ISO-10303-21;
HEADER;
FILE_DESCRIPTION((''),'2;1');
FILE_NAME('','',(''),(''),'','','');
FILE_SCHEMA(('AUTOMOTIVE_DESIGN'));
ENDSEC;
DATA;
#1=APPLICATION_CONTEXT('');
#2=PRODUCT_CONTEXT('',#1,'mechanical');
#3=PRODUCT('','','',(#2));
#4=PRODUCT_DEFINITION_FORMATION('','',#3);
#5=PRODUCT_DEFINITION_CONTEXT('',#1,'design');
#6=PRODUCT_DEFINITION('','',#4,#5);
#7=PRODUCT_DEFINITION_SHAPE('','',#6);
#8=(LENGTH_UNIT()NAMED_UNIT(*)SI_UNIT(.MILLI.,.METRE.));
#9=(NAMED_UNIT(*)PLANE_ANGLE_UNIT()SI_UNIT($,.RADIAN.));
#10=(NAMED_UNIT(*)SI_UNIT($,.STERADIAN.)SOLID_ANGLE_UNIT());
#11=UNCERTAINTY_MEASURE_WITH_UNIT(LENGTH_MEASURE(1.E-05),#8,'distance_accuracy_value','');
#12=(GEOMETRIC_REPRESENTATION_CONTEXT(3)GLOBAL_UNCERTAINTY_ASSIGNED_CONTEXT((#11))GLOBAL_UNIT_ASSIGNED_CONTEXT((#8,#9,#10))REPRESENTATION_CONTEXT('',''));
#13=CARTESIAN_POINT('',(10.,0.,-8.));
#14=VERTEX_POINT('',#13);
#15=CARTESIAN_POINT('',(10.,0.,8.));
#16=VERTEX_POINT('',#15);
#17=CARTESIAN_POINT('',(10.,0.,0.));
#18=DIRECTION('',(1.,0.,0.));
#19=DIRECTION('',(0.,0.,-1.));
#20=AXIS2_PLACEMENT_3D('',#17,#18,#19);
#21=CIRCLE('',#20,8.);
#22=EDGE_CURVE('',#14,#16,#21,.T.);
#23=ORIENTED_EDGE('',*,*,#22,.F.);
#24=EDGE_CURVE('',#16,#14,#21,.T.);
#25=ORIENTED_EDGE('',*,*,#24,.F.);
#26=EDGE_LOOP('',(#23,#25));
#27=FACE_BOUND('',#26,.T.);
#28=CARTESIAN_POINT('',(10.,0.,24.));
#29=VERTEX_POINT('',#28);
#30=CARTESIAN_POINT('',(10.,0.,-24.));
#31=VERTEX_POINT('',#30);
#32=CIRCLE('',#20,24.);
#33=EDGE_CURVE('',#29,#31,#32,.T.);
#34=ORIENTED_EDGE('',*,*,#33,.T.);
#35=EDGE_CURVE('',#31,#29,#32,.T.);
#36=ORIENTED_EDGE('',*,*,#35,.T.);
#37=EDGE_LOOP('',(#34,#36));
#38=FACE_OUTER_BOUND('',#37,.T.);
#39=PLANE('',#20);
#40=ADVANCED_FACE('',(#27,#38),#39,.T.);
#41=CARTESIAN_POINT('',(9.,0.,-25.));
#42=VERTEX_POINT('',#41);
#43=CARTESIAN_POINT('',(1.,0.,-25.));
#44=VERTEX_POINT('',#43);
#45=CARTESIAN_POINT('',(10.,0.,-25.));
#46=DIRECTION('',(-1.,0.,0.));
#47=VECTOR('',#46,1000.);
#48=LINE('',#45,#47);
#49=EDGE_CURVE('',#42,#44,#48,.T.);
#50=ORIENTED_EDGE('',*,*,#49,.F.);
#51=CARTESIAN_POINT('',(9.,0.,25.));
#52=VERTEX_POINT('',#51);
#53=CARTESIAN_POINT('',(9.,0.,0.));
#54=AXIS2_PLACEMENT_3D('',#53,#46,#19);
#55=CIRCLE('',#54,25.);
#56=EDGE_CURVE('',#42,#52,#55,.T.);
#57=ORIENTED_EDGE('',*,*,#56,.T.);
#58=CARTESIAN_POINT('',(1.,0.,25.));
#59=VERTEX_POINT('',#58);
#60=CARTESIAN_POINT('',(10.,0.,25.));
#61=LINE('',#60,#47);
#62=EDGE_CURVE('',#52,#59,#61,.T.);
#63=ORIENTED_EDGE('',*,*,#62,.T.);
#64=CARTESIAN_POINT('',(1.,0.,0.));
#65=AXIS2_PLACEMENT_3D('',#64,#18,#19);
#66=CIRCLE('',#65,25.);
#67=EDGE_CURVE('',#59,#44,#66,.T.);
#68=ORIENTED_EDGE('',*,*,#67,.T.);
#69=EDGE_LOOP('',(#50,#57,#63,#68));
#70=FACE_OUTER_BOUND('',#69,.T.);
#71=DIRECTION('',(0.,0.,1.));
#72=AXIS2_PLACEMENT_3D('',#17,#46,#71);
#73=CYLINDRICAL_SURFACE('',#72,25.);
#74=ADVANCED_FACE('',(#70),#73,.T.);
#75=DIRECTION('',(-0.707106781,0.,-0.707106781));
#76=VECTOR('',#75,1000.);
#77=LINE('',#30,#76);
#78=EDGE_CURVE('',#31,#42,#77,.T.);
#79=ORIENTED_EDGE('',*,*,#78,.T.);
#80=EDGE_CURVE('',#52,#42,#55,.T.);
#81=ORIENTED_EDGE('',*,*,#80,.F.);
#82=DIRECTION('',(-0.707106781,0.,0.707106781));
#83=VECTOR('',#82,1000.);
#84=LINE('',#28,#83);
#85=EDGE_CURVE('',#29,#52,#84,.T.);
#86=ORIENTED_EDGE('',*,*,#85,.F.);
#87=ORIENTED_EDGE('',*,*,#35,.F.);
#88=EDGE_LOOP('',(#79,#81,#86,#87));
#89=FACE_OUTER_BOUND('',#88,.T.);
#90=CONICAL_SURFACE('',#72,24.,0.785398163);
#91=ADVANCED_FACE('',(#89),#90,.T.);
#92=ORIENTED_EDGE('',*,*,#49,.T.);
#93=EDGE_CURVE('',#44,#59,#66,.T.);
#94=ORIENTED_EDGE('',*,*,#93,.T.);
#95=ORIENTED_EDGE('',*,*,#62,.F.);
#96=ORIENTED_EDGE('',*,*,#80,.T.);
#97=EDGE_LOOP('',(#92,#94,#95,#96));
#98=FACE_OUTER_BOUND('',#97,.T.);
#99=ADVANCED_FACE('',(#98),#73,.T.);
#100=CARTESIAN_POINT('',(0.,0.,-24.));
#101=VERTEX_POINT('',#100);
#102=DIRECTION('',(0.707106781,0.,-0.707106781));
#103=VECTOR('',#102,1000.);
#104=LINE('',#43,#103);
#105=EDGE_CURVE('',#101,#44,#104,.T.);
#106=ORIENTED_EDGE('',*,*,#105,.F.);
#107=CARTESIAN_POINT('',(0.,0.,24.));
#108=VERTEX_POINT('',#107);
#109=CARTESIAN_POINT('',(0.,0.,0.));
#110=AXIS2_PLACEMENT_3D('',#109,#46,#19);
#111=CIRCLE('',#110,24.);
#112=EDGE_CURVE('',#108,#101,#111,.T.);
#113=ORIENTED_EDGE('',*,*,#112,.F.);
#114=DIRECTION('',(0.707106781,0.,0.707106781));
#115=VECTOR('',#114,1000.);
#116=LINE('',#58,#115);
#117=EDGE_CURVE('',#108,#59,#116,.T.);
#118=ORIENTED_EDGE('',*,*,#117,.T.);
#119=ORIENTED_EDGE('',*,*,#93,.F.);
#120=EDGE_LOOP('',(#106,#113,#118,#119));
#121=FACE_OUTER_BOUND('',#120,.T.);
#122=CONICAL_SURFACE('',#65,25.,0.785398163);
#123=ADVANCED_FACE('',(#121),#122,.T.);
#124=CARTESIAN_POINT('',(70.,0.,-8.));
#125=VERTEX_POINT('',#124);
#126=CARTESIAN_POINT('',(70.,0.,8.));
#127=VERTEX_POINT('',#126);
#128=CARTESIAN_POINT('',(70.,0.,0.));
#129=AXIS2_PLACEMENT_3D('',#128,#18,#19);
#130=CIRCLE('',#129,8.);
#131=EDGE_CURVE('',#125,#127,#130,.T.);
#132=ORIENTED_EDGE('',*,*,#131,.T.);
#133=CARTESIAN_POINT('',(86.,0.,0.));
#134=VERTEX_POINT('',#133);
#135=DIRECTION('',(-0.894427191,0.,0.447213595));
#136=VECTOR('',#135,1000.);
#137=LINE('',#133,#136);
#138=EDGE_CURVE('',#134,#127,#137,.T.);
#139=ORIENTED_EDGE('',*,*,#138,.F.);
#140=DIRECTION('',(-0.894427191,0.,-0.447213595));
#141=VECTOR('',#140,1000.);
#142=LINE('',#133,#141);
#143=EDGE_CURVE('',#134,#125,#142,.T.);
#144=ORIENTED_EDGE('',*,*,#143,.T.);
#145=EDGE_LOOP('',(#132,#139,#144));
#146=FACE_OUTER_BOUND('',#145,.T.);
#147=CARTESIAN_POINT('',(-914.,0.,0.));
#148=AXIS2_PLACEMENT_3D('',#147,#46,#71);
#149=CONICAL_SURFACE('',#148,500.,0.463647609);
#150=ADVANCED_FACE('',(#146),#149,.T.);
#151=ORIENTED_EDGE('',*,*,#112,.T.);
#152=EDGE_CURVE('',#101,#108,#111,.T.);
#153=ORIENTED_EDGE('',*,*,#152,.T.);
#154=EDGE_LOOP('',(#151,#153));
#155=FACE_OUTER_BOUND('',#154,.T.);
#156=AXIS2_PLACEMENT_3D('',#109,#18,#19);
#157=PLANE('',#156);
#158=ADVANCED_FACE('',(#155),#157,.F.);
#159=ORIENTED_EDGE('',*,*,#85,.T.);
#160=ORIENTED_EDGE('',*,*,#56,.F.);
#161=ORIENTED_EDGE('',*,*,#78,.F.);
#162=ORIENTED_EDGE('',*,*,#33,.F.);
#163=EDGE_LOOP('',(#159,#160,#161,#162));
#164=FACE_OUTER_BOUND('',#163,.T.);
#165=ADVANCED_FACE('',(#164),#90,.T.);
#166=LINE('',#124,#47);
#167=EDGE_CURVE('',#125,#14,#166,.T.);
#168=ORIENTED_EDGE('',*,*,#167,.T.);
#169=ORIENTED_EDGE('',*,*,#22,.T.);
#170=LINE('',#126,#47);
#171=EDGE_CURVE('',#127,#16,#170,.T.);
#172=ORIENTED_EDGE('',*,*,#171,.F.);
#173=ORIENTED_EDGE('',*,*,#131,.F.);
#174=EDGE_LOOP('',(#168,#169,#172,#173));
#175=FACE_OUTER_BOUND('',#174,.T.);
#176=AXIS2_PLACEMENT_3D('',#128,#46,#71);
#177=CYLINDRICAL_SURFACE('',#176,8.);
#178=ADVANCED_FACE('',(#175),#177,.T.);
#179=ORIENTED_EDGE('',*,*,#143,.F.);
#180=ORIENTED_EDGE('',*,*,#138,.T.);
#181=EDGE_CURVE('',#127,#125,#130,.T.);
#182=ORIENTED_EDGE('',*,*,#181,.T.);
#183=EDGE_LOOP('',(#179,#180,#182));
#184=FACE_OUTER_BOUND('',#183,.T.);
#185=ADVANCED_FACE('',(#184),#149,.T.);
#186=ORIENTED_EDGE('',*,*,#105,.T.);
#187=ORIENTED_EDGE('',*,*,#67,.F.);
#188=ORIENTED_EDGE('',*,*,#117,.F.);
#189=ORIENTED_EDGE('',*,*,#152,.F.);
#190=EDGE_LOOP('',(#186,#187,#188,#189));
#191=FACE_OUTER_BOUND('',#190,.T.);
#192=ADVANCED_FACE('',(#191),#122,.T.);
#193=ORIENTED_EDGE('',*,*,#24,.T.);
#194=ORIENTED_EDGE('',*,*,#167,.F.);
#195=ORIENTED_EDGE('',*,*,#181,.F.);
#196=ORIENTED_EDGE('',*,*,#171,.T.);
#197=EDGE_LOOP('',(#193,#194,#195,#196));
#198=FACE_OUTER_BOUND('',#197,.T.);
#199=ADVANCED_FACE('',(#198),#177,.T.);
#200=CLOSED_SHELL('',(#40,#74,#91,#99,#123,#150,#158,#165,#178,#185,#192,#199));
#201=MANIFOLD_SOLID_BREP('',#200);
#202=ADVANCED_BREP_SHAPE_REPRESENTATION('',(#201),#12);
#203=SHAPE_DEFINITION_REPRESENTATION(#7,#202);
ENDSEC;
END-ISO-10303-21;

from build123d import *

# Parameters (mm, degrees)
SKETCH_1_R      = 25
EXTRUDE_1_DEPTH = 10
SKETCH_2_R      = 8
EXTRUDE_2_DEPTH = 60
CHAMFER_1_SIZE  = 1


with BuildPart() as part:
    # 草图1 → 凸台-拉伸1 (new body)
    with BuildSketch(Plane(origin=(0, 0, 0), x_dir=(0, 0, -1), z_dir=(1, 0, 0))):
        Circle(SKETCH_1_R)
    extrude(amount=EXTRUDE_1_DEPTH)

    # 草图2 → 凸台-拉伸2 (add)
    with BuildSketch(Plane(origin=(10, 0, 0), x_dir=(0, 0, -1), z_dir=(1, 0, 0))):
        Circle(SKETCH_2_R)
    extrude(amount=EXTRUDE_2_DEPTH)

    # 草图3 → 旋转1 (revolve)
    with BuildSketch(Plane.XY, mode=Mode.PRIVATE) as revolve_1_sk:
        Polygon((70, 8), (86, 0), (70, 0), align=None)
    revolve(revolve_1_sk.sketch.rotate(Axis((0, 0, 0), (1, 0, 0)), 90), axis=Axis((0, 0, 0), (1, 0, 0)))

    # 倒角1
    chamfer_1_edges = [part.edges().sort_by_distance(p)[0] for p in [
        (0, 0, 25),
        (10, 0, 25),
    ]]
    chamfer(chamfer_1_edges, length=CHAMFER_1_SIZE)


solid = part.part
